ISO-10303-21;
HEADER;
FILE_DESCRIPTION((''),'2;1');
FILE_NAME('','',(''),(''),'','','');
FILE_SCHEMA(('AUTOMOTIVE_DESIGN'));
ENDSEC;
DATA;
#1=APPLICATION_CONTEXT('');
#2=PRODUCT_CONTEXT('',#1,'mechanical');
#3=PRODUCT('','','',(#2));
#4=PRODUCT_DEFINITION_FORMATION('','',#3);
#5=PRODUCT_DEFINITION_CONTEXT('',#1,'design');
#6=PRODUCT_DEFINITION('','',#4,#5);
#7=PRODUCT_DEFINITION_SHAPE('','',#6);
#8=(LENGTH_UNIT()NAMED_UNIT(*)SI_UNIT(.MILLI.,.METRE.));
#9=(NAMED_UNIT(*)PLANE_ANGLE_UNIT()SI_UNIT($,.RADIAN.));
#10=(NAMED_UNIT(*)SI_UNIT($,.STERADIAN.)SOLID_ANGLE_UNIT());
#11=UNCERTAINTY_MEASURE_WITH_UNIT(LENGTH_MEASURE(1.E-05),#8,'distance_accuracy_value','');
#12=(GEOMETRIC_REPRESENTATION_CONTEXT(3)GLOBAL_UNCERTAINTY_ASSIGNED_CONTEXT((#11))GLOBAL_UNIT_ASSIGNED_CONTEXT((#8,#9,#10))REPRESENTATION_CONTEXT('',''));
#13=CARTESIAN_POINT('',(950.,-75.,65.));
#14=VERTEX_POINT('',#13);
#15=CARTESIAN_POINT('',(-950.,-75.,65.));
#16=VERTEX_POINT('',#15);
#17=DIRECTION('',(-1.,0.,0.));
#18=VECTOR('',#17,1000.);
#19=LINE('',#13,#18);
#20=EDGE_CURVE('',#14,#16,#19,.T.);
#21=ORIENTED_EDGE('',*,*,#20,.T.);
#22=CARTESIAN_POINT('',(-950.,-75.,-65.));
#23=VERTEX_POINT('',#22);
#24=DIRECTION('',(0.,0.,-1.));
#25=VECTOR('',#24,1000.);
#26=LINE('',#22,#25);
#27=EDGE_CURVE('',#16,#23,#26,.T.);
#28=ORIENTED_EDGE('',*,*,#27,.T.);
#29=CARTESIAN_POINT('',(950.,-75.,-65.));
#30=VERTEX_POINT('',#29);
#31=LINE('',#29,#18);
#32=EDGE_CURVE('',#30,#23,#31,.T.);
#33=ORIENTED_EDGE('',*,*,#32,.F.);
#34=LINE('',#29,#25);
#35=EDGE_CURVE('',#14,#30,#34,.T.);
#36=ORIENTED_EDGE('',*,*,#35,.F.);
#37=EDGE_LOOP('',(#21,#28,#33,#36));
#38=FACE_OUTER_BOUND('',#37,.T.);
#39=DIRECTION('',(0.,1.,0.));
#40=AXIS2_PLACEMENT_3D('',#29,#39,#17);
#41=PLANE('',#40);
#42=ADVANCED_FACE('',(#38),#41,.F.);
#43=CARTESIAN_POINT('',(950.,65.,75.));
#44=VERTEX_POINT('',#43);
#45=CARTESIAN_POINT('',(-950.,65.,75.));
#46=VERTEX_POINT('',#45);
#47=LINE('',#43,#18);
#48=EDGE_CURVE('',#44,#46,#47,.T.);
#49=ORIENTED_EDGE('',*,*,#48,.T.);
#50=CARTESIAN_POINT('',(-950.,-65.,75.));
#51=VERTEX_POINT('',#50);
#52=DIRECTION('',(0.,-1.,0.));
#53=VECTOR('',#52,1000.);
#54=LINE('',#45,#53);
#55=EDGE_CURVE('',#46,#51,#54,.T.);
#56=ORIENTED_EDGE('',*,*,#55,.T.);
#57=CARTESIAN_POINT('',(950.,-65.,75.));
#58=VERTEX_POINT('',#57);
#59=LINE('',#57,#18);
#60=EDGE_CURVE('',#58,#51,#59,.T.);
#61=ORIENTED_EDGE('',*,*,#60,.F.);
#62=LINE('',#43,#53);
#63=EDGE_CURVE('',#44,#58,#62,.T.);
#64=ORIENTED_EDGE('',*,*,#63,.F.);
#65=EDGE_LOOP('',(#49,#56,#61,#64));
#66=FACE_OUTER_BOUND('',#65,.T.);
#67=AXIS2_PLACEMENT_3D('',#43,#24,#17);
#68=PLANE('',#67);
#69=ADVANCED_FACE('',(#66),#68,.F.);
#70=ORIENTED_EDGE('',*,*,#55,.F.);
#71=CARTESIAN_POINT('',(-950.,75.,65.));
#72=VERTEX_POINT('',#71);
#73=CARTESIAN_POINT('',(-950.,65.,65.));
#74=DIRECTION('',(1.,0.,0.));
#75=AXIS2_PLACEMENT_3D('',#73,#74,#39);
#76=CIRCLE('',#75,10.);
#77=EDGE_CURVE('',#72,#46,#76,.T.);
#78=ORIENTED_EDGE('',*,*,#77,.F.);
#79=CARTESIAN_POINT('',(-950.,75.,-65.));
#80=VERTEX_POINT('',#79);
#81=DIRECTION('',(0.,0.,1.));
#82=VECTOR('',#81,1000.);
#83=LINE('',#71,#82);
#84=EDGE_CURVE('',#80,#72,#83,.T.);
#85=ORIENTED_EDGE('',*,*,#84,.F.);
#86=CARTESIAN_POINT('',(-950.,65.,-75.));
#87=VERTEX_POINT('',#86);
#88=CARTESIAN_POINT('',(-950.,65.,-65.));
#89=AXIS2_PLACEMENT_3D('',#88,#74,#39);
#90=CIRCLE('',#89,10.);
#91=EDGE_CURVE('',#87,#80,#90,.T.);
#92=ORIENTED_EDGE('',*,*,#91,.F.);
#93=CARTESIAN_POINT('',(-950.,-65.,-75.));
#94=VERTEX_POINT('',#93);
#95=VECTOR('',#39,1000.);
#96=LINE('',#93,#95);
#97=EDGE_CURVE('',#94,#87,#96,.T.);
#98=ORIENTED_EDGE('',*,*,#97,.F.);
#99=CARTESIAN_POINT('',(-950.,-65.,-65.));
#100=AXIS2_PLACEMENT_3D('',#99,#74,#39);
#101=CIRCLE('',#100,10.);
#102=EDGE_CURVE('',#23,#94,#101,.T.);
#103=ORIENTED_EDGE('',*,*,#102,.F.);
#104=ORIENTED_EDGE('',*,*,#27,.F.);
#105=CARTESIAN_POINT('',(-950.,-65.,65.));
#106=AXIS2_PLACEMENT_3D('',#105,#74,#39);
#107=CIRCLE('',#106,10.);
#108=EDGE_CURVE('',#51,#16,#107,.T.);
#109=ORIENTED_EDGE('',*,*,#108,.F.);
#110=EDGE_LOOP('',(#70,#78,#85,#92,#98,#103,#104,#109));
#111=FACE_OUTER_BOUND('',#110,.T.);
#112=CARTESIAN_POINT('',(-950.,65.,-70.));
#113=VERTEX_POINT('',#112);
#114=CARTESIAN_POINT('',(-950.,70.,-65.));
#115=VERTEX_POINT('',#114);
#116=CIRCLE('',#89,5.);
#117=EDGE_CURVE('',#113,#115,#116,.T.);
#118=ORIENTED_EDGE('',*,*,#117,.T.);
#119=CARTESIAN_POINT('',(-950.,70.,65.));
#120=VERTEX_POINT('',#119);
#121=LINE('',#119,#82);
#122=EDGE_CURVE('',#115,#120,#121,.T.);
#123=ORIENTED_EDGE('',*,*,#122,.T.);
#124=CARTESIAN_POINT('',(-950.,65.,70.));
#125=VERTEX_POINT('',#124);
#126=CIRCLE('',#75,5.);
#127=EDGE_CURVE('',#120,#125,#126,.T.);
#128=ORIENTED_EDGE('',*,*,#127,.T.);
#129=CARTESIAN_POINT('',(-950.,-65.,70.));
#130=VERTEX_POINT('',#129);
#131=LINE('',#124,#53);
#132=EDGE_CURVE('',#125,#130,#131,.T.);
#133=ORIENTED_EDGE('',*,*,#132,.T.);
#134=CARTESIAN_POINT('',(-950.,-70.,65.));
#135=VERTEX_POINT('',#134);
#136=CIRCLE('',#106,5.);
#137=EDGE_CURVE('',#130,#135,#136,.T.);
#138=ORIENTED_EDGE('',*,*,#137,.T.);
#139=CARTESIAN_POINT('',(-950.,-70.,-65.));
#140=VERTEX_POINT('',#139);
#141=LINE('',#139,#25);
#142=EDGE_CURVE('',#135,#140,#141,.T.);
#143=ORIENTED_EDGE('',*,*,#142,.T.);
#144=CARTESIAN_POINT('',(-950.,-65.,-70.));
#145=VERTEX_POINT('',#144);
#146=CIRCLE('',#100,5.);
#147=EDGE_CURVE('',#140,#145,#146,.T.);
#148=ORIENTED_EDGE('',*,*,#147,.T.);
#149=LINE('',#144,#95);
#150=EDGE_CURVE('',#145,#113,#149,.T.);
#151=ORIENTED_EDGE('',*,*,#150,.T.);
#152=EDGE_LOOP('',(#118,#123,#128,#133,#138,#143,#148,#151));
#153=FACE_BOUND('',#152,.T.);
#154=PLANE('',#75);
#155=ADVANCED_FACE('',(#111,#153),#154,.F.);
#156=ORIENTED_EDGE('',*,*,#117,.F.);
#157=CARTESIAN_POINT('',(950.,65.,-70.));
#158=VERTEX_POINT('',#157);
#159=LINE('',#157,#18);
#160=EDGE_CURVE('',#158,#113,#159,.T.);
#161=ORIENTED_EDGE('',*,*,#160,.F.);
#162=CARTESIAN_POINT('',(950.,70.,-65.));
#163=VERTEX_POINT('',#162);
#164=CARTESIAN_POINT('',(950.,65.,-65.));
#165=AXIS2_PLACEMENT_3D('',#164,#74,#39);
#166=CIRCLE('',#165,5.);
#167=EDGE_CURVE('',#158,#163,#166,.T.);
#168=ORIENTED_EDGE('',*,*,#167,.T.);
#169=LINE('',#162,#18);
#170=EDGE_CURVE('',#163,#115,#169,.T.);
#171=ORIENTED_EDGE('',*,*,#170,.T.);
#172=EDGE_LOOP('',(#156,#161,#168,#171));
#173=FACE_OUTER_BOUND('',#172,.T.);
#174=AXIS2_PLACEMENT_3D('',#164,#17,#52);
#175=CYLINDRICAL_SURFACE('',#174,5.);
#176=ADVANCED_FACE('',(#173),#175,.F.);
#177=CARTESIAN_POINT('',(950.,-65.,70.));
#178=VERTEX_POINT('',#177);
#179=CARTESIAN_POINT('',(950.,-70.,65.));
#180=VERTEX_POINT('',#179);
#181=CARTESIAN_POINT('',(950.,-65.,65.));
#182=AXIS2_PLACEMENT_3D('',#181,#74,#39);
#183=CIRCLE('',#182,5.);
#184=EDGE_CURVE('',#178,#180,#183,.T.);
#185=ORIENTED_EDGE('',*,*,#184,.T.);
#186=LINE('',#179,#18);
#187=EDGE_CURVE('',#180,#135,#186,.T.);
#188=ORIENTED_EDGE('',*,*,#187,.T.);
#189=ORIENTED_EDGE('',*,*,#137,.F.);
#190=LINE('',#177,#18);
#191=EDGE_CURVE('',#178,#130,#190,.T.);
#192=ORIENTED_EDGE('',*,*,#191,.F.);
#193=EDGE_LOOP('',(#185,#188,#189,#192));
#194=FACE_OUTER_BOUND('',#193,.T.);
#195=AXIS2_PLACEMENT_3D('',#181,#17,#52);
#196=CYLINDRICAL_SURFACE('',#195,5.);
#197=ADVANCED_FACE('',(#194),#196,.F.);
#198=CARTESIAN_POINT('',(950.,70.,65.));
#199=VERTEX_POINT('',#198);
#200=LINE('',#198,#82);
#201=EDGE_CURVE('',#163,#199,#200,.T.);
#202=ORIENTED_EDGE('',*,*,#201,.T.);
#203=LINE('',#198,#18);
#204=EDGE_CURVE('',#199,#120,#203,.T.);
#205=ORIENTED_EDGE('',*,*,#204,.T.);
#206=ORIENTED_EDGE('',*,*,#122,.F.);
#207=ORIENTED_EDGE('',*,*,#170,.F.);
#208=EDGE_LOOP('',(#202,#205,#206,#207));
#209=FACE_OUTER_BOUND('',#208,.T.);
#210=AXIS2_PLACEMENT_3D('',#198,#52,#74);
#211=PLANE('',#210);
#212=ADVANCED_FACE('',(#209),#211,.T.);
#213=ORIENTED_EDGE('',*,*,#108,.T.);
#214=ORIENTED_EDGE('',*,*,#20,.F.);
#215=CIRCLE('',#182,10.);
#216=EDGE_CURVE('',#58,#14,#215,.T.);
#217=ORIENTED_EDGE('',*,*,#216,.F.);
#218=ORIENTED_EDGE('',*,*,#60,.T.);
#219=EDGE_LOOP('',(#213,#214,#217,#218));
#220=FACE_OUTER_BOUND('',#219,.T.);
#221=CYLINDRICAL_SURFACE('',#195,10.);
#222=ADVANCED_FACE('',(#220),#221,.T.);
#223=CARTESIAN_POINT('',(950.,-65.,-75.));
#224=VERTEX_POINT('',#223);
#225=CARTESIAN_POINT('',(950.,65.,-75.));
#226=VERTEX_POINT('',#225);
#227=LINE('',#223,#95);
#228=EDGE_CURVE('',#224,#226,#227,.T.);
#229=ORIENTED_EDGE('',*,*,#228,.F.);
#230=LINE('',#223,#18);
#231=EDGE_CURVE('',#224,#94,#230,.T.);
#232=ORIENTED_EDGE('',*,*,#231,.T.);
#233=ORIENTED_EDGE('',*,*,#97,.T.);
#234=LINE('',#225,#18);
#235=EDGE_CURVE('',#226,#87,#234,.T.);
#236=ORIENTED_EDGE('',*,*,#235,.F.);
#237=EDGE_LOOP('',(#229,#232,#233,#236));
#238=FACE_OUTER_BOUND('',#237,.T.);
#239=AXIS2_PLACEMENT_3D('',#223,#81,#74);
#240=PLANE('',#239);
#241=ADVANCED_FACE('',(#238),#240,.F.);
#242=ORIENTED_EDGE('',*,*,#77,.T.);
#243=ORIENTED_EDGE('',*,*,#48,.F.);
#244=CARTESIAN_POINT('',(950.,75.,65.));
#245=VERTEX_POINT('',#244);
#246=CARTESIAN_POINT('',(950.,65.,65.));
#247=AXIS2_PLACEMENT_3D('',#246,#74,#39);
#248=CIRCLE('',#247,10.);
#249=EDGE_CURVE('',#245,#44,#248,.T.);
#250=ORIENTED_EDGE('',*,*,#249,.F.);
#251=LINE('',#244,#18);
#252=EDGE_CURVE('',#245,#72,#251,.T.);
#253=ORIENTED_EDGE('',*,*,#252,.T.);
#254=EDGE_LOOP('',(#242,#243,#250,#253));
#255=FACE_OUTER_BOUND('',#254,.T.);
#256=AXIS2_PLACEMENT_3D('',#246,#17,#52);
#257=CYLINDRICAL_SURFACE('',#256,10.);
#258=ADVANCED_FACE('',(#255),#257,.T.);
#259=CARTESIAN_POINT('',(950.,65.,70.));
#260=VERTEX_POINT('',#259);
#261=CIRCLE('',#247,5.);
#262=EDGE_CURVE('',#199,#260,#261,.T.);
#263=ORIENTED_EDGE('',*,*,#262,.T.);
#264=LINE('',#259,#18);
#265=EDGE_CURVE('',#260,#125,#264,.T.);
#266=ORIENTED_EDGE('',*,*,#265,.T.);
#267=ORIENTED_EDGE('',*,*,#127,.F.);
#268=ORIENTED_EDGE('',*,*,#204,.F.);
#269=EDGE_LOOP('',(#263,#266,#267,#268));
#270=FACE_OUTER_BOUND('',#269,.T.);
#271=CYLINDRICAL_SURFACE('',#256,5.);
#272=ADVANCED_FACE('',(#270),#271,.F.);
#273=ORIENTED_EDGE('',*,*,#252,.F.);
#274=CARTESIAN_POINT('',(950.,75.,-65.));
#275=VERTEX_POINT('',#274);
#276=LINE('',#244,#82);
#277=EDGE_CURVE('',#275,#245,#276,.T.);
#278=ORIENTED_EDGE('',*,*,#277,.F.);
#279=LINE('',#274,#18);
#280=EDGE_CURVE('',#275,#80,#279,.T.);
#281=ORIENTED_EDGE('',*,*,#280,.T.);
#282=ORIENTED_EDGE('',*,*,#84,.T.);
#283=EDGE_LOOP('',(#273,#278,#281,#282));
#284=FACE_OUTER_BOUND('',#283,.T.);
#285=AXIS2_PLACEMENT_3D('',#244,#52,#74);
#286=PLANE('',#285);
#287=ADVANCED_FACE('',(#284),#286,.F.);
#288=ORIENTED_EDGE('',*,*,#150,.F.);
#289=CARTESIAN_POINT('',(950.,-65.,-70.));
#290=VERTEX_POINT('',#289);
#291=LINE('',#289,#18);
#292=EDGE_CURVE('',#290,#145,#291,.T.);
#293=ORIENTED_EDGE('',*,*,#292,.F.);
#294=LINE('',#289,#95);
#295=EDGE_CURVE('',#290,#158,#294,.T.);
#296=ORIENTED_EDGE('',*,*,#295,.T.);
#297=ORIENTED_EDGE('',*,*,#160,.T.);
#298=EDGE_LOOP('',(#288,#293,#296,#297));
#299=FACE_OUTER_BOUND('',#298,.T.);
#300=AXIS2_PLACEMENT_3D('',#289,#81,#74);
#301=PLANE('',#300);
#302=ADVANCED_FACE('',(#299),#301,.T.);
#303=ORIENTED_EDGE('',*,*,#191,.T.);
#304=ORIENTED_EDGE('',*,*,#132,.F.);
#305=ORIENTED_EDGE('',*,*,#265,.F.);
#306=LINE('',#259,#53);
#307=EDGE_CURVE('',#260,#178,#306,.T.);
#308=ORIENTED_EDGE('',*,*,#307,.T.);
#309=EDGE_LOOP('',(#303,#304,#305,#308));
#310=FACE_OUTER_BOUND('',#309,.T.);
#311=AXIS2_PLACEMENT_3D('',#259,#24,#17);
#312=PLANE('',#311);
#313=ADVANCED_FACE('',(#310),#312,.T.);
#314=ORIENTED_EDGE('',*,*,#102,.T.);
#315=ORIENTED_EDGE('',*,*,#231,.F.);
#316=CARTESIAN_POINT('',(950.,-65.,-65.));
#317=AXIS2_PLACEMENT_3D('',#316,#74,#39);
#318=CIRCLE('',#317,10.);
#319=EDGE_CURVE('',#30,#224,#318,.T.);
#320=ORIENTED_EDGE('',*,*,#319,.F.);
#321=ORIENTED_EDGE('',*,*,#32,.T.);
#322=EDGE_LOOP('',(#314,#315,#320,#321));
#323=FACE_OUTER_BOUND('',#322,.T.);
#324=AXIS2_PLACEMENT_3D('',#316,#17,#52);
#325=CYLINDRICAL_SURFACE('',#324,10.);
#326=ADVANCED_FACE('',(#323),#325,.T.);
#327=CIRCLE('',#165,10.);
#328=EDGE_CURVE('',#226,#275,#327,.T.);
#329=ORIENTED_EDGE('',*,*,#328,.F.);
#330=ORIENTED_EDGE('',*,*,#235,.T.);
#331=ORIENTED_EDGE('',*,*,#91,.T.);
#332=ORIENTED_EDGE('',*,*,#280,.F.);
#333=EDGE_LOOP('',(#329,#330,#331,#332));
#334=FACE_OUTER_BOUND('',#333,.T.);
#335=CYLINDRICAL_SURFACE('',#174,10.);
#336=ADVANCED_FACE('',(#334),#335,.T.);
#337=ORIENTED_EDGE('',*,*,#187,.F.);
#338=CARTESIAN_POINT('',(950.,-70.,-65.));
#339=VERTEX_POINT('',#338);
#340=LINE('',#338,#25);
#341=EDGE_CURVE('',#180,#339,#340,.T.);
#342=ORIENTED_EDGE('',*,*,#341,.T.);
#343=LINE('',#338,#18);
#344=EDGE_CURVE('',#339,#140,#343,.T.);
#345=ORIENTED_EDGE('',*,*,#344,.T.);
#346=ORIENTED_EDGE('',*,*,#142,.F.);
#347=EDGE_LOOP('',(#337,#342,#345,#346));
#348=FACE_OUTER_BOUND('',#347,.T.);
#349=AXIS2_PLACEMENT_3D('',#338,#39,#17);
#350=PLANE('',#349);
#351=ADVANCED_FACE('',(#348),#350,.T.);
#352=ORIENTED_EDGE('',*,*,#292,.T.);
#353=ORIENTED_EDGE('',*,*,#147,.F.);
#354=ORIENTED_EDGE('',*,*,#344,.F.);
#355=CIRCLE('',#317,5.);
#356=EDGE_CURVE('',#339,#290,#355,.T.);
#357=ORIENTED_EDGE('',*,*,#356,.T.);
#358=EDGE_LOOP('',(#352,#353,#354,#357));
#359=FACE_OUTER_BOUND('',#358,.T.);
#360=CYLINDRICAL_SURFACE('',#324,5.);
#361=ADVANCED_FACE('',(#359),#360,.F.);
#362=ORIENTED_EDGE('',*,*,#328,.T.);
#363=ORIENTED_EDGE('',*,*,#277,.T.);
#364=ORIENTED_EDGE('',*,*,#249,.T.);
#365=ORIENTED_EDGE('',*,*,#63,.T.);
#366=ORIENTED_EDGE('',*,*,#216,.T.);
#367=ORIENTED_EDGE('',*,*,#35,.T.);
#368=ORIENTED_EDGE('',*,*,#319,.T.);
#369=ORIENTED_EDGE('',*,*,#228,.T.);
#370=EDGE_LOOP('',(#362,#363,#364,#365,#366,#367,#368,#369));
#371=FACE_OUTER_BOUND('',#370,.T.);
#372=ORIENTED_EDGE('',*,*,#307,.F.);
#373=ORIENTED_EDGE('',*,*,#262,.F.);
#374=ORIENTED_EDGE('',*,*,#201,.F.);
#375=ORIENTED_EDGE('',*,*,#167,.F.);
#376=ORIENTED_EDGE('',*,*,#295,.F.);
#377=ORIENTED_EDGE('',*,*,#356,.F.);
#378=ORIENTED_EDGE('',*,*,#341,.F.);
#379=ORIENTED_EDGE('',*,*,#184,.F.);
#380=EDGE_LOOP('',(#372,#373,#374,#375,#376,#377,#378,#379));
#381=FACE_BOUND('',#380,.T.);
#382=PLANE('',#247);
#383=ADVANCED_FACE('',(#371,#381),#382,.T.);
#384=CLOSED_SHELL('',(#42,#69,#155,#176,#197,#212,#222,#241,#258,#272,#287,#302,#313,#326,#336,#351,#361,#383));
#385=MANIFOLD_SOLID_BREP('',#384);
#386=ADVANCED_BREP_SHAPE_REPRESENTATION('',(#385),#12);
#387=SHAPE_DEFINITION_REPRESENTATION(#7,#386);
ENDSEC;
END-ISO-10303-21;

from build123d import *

# Parameters (mm, degrees)
GB_6728_1986_150_X_150_X_5_1_DEPTH = 1900


with BuildPart() as part:
    # Sketch1 → Gb／6728-1986方形空心型钢 150 X 150 X 5(1) (new body)
    with BuildSketch(Plane.YZ.offset(-950)):
        with BuildLine():
            Line((-65, -75), (65, -75))
            ThreePointArc((65, -75), (72.071067812, -72.071067812), (75, -65))
            Line((75, -65), (75, 65))
            ThreePointArc((75, 65), (72.071067812, 72.071067812), (65, 75))
            Line((65, 75), (-65, 75))
            ThreePointArc((-65, 75), (-72.071067812, 72.071067812), (-75, 65))
            Line((-75, 65), (-75, -65))
            ThreePointArc((-75, -65), (-72.071067812, -72.071067812), (-65, -75))
        make_face()
        with BuildLine():
            Line((-65, -70), (65, -70))
            ThreePointArc((65, -70), (68.535533906, -68.535533906), (70, -65))
            Line((70, -65), (70, 65))
            ThreePointArc((70, 65), (68.535533906, 68.535533906), (65, 70))
            Line((65, 70), (-65, 70))
            ThreePointArc((-65, 70), (-68.535533906, 68.535533906), (-70, 65))
            Line((-70, 65), (-70, -65))
            ThreePointArc((-70, -65), (-68.535533906, -68.535533906), (-65, -70))
        make_face(mode=Mode.SUBTRACT)
    extrude(amount=GB_6728_1986_150_X_150_X_5_1_DEPTH)


solid = part.part
